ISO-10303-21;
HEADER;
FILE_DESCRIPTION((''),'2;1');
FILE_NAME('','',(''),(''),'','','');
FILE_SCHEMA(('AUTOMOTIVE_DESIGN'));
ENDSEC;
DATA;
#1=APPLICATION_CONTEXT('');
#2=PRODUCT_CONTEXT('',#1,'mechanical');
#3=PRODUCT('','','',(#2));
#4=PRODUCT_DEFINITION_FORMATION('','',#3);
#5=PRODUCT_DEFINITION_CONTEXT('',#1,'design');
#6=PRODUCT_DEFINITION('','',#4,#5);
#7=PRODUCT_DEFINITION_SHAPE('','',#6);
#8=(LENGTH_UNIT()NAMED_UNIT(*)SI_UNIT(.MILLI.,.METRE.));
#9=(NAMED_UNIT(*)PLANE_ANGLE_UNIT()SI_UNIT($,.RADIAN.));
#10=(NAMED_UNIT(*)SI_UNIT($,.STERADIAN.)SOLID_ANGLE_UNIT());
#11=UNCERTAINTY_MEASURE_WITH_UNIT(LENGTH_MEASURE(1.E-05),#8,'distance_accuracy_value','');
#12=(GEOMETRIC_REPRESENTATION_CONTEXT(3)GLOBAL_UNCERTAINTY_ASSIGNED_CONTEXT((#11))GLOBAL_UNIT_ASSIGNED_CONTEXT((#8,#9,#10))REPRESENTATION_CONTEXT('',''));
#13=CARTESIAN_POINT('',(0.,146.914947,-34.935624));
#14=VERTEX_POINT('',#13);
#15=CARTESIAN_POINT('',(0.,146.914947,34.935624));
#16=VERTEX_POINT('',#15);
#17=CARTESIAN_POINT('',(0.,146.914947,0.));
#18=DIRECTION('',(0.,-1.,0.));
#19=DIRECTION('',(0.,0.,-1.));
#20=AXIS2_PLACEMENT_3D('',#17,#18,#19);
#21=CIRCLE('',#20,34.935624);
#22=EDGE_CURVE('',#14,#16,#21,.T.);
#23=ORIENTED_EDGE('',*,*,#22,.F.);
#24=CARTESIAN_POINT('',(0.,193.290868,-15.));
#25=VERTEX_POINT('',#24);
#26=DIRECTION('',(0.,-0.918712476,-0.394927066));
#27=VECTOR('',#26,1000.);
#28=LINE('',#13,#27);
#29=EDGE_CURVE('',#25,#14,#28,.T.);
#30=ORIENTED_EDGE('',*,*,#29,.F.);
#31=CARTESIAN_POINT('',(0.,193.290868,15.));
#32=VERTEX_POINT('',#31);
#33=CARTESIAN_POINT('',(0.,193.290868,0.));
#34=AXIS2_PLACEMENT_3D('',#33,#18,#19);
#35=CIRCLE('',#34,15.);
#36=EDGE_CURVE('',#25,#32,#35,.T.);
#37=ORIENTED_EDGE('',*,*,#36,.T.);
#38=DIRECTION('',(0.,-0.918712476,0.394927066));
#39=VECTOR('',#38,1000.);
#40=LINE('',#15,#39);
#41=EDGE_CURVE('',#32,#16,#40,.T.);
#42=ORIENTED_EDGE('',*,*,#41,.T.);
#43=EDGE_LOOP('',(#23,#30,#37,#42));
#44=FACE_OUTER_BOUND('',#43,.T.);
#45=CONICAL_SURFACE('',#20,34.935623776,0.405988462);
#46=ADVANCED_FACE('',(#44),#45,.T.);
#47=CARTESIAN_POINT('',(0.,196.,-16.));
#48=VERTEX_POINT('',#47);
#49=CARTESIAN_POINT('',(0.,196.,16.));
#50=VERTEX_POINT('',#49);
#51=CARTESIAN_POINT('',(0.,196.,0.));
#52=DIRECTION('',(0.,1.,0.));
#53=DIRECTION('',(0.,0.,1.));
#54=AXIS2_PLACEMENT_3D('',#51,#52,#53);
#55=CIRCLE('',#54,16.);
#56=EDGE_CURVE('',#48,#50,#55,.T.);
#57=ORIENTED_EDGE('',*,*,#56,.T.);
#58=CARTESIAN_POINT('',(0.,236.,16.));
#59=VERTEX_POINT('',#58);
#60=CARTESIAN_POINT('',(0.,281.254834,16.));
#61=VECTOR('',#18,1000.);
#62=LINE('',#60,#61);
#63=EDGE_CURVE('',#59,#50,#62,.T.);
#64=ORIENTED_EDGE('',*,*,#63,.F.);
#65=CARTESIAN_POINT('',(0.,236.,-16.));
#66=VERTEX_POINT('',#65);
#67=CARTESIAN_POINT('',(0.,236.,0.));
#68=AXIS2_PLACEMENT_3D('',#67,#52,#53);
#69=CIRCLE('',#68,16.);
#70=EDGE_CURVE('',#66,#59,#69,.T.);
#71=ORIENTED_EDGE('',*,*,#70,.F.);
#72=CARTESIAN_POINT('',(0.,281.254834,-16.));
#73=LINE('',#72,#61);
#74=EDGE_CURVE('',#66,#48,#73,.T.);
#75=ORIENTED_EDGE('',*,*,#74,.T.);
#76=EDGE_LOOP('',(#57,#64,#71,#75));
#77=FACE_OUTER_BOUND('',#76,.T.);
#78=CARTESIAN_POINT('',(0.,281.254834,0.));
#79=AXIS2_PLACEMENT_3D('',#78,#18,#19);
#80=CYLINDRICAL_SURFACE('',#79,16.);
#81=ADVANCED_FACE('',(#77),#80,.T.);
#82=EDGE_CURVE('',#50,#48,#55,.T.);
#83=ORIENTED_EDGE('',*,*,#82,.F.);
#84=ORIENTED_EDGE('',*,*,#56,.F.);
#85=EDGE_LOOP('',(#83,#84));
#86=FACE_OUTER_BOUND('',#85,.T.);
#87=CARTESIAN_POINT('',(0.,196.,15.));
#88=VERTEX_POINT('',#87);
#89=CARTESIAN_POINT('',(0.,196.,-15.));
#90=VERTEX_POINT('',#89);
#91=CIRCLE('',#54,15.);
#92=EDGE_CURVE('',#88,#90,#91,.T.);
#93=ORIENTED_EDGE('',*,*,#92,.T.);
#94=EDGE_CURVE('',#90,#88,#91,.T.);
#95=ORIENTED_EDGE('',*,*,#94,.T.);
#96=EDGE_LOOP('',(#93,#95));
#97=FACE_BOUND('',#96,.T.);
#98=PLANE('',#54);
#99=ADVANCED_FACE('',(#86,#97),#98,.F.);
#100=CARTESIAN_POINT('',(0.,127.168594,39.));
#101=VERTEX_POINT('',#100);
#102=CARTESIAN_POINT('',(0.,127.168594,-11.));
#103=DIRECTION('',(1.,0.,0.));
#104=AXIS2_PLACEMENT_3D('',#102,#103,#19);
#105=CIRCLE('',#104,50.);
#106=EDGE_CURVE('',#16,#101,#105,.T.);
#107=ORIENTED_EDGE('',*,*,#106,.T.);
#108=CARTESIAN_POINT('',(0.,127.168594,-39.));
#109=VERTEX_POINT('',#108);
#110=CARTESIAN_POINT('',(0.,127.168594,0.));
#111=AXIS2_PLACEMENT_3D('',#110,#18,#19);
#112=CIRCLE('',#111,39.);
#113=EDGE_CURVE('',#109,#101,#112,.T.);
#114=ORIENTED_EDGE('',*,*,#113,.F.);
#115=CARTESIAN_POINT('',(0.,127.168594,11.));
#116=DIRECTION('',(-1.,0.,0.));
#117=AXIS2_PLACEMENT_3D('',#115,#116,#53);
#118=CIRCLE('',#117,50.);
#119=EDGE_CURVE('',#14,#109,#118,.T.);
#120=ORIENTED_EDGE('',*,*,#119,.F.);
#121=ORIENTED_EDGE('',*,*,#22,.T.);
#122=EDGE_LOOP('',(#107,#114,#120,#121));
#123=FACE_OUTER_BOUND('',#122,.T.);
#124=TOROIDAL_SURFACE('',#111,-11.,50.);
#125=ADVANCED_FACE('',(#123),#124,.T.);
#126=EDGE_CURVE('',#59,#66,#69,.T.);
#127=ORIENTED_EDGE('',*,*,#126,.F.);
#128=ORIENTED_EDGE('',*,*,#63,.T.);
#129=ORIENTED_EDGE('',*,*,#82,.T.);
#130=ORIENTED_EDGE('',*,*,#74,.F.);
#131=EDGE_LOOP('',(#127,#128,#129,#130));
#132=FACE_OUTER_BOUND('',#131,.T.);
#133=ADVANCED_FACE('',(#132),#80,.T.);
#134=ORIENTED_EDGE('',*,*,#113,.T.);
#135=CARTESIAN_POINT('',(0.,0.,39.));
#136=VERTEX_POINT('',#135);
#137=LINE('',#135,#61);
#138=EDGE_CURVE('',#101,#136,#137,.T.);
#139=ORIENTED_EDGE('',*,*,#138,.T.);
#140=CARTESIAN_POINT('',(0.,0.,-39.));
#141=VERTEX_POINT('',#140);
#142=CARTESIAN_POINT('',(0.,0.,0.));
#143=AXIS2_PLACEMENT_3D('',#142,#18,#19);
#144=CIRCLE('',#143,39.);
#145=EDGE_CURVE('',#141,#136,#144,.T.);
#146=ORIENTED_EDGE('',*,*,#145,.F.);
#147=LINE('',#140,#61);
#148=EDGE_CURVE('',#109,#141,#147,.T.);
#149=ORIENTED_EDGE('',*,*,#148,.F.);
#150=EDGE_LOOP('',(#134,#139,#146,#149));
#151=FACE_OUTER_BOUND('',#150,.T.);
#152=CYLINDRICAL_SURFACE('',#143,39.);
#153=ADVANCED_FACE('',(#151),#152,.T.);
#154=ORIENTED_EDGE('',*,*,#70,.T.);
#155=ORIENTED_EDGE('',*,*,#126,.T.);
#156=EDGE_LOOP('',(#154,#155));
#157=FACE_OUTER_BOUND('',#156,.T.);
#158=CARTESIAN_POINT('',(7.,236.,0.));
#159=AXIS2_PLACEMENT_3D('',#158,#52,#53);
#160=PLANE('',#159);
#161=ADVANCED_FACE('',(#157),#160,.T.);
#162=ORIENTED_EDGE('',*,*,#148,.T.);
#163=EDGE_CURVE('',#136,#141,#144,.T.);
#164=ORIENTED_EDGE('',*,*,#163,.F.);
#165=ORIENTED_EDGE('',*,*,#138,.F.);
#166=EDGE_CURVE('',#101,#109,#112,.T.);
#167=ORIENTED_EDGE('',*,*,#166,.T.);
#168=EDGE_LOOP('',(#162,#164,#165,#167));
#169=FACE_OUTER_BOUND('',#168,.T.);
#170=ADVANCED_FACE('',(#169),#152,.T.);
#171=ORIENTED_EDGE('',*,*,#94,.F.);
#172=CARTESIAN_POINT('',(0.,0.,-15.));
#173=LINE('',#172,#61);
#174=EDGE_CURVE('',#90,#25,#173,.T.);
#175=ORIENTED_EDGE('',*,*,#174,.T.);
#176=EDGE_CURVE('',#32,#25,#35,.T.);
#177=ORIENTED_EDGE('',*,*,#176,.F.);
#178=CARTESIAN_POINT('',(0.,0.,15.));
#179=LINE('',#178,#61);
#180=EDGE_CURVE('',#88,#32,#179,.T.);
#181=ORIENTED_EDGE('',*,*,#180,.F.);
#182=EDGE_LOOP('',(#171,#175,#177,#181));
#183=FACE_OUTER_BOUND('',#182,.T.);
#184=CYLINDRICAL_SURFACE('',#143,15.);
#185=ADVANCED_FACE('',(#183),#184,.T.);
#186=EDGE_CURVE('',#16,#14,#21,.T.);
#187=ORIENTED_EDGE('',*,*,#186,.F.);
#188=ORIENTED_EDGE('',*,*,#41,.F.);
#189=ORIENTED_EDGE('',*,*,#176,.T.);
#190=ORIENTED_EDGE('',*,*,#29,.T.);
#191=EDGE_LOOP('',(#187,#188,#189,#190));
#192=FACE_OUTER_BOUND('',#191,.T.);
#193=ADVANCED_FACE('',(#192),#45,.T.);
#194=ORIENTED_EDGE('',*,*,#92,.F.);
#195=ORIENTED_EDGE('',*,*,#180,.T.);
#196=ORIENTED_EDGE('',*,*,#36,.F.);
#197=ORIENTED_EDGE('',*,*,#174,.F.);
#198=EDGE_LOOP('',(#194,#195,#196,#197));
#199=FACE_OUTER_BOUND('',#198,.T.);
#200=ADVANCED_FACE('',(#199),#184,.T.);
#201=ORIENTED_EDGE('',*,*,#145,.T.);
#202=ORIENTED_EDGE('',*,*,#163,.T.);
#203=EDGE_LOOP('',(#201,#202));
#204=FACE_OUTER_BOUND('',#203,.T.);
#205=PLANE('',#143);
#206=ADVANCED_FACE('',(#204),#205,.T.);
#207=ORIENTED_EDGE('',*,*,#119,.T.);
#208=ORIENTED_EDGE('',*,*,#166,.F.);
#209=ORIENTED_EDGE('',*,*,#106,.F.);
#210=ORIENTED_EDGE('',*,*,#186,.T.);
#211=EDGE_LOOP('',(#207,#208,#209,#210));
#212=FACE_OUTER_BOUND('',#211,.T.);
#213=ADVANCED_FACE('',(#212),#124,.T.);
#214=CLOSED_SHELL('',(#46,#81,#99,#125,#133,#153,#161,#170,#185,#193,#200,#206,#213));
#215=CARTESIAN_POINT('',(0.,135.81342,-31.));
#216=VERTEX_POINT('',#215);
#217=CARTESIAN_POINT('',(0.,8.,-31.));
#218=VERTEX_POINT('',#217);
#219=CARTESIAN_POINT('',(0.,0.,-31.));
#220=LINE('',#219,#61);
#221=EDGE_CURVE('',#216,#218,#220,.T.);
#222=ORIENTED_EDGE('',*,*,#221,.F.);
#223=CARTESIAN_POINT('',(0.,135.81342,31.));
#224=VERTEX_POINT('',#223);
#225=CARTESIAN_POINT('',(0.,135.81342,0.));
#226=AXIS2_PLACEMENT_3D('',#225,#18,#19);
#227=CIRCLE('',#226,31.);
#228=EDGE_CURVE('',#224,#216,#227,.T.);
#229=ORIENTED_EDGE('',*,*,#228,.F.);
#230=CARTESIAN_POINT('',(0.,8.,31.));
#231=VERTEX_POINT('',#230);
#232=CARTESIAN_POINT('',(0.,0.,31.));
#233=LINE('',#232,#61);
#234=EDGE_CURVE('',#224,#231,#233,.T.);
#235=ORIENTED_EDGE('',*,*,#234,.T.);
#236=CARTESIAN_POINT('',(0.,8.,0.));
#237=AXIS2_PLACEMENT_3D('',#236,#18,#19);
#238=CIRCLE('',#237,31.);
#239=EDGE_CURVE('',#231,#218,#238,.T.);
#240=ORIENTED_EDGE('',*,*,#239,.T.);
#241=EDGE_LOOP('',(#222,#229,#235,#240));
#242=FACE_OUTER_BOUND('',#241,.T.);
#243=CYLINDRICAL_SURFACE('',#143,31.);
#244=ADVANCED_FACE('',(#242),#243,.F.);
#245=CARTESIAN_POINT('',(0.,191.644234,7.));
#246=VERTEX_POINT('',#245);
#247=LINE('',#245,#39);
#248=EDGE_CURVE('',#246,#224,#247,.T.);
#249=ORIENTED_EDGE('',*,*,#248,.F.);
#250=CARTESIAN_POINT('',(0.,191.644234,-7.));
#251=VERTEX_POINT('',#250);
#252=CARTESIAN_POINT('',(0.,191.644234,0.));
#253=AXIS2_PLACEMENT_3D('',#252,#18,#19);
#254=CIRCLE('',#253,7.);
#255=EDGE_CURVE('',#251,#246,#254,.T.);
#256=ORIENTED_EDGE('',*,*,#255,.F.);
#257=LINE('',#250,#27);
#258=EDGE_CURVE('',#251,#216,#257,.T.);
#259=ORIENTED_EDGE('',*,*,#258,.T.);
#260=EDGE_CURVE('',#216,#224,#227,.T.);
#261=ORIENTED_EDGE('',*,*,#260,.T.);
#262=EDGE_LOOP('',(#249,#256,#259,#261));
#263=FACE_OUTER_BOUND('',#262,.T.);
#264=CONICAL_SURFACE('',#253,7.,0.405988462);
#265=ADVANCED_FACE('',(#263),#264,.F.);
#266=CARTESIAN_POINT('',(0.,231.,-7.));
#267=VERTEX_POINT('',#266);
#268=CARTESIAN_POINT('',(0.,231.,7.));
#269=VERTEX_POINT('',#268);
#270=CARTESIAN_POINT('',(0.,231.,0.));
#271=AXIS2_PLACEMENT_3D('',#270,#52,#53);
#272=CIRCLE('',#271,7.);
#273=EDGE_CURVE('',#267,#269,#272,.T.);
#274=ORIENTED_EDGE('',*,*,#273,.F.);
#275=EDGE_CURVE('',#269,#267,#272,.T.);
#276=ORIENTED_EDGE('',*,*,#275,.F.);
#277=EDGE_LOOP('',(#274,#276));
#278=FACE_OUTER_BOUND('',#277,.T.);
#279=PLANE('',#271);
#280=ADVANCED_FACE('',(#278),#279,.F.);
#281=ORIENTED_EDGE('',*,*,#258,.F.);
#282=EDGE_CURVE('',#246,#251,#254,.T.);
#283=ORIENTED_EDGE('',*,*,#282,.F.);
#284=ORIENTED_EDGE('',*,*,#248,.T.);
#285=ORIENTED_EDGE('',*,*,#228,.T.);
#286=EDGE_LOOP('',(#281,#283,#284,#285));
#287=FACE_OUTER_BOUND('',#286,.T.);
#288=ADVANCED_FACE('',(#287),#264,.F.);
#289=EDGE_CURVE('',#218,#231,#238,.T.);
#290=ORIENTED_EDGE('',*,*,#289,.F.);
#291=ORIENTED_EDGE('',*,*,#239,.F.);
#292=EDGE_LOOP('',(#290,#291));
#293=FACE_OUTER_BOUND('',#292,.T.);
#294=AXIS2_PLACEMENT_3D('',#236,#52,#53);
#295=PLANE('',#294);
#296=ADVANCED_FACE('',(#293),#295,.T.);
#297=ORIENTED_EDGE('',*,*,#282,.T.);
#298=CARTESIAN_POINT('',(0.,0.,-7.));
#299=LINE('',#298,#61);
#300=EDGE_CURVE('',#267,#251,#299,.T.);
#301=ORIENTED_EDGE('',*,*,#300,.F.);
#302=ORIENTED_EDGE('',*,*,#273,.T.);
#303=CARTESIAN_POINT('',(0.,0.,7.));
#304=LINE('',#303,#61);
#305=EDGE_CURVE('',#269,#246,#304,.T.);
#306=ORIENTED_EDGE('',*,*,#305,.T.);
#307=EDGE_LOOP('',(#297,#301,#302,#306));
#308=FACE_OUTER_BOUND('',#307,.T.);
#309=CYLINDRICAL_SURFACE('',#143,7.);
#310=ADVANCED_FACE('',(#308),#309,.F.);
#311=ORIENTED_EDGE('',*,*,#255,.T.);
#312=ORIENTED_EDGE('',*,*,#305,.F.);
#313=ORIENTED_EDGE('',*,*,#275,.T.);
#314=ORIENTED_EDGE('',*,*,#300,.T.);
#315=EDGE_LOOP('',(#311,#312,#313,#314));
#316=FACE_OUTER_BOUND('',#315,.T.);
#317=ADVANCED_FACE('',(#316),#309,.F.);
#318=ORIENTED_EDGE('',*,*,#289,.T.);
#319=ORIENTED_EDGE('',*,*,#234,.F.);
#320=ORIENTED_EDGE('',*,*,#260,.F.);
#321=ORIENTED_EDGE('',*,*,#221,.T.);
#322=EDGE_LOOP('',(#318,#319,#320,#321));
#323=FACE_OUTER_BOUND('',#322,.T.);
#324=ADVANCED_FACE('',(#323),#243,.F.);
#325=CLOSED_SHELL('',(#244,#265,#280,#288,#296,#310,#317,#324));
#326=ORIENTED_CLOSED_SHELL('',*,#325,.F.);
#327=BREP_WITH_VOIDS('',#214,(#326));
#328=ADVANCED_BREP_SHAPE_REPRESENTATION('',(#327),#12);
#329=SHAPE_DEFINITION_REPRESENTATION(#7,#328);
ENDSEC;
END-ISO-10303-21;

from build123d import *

# Parameters (mm, degrees)
BOSS_EXTRUDE1_START = -5
SKETCH2_R           = 7
BOSS_EXTRUDE1_DEPTH = 5
BOSS_EXTRUDE2_START = 40
SKETCH3_R           = 16
SKETCH3_R_2         = 15
BOSS_EXTRUDE2_DEPTH = 40


with BuildPart() as part:
    # Sketch1 → Revolve1 (revolve)
    with BuildSketch(Plane.XY, mode=Mode.PRIVATE) as revolve1_sk:
        with BuildLine():
            Line((0, 0), (39, 0))
            Line((39, 0), (39, 127.168593742))
            ThreePointArc((39, 127.168593742), (37.973366174, 137.248742828), (34.935623776, 146.914947034))
            Line((34.935623776, 146.914947034), (15, 193.29086769))
            Line((15, 193.29086769), (15, 236))
            Line((15, 236), (7, 236))
            Line((7, 236), (7, 191.64423404))
            Line((7, 191.64423404), (31, 135.813420404))
            Line((31, 135.813420404), (31, 8))
            Line((31, 8), (0, 8))
            Line((0, 8), (0, 0))
        make_face()
    revolve(revolve1_sk.sketch.rotate(Axis((0, 0, 0), (0, 1, 0)), 90), axis=Axis((0, 0, 0), (0, 1, 0)))

    # Sketch2 → Boss-Extrude1 (add)
    with BuildSketch(Plane(origin=(0, 236, 0), x_dir=(1, 0, 0), z_dir=(0, 1, 0)).offset(BOSS_EXTRUDE1_START)):
        with Locations(Location((0, 0, 0), (0, 0, 90))):
            Circle(SKETCH2_R)
    extrude(amount=BOSS_EXTRUDE1_DEPTH)

    # Sketch3 → Boss-Extrude2 (add)
    with BuildSketch(Plane(origin=(0, 196, 0), x_dir=(1, 0, 0), z_dir=(0, 1, 0)).offset(BOSS_EXTRUDE2_START)):
        with Locations(Location((0, 0, 0), (0, 0, 270))):
            Circle(SKETCH3_R)
        with Locations(Location((0, 0, 0), (0, 0, 90))):
            Circle(SKETCH3_R_2, mode=Mode.SUBTRACT)
    extrude(amount=-BOSS_EXTRUDE2_DEPTH)


solid = part.part
